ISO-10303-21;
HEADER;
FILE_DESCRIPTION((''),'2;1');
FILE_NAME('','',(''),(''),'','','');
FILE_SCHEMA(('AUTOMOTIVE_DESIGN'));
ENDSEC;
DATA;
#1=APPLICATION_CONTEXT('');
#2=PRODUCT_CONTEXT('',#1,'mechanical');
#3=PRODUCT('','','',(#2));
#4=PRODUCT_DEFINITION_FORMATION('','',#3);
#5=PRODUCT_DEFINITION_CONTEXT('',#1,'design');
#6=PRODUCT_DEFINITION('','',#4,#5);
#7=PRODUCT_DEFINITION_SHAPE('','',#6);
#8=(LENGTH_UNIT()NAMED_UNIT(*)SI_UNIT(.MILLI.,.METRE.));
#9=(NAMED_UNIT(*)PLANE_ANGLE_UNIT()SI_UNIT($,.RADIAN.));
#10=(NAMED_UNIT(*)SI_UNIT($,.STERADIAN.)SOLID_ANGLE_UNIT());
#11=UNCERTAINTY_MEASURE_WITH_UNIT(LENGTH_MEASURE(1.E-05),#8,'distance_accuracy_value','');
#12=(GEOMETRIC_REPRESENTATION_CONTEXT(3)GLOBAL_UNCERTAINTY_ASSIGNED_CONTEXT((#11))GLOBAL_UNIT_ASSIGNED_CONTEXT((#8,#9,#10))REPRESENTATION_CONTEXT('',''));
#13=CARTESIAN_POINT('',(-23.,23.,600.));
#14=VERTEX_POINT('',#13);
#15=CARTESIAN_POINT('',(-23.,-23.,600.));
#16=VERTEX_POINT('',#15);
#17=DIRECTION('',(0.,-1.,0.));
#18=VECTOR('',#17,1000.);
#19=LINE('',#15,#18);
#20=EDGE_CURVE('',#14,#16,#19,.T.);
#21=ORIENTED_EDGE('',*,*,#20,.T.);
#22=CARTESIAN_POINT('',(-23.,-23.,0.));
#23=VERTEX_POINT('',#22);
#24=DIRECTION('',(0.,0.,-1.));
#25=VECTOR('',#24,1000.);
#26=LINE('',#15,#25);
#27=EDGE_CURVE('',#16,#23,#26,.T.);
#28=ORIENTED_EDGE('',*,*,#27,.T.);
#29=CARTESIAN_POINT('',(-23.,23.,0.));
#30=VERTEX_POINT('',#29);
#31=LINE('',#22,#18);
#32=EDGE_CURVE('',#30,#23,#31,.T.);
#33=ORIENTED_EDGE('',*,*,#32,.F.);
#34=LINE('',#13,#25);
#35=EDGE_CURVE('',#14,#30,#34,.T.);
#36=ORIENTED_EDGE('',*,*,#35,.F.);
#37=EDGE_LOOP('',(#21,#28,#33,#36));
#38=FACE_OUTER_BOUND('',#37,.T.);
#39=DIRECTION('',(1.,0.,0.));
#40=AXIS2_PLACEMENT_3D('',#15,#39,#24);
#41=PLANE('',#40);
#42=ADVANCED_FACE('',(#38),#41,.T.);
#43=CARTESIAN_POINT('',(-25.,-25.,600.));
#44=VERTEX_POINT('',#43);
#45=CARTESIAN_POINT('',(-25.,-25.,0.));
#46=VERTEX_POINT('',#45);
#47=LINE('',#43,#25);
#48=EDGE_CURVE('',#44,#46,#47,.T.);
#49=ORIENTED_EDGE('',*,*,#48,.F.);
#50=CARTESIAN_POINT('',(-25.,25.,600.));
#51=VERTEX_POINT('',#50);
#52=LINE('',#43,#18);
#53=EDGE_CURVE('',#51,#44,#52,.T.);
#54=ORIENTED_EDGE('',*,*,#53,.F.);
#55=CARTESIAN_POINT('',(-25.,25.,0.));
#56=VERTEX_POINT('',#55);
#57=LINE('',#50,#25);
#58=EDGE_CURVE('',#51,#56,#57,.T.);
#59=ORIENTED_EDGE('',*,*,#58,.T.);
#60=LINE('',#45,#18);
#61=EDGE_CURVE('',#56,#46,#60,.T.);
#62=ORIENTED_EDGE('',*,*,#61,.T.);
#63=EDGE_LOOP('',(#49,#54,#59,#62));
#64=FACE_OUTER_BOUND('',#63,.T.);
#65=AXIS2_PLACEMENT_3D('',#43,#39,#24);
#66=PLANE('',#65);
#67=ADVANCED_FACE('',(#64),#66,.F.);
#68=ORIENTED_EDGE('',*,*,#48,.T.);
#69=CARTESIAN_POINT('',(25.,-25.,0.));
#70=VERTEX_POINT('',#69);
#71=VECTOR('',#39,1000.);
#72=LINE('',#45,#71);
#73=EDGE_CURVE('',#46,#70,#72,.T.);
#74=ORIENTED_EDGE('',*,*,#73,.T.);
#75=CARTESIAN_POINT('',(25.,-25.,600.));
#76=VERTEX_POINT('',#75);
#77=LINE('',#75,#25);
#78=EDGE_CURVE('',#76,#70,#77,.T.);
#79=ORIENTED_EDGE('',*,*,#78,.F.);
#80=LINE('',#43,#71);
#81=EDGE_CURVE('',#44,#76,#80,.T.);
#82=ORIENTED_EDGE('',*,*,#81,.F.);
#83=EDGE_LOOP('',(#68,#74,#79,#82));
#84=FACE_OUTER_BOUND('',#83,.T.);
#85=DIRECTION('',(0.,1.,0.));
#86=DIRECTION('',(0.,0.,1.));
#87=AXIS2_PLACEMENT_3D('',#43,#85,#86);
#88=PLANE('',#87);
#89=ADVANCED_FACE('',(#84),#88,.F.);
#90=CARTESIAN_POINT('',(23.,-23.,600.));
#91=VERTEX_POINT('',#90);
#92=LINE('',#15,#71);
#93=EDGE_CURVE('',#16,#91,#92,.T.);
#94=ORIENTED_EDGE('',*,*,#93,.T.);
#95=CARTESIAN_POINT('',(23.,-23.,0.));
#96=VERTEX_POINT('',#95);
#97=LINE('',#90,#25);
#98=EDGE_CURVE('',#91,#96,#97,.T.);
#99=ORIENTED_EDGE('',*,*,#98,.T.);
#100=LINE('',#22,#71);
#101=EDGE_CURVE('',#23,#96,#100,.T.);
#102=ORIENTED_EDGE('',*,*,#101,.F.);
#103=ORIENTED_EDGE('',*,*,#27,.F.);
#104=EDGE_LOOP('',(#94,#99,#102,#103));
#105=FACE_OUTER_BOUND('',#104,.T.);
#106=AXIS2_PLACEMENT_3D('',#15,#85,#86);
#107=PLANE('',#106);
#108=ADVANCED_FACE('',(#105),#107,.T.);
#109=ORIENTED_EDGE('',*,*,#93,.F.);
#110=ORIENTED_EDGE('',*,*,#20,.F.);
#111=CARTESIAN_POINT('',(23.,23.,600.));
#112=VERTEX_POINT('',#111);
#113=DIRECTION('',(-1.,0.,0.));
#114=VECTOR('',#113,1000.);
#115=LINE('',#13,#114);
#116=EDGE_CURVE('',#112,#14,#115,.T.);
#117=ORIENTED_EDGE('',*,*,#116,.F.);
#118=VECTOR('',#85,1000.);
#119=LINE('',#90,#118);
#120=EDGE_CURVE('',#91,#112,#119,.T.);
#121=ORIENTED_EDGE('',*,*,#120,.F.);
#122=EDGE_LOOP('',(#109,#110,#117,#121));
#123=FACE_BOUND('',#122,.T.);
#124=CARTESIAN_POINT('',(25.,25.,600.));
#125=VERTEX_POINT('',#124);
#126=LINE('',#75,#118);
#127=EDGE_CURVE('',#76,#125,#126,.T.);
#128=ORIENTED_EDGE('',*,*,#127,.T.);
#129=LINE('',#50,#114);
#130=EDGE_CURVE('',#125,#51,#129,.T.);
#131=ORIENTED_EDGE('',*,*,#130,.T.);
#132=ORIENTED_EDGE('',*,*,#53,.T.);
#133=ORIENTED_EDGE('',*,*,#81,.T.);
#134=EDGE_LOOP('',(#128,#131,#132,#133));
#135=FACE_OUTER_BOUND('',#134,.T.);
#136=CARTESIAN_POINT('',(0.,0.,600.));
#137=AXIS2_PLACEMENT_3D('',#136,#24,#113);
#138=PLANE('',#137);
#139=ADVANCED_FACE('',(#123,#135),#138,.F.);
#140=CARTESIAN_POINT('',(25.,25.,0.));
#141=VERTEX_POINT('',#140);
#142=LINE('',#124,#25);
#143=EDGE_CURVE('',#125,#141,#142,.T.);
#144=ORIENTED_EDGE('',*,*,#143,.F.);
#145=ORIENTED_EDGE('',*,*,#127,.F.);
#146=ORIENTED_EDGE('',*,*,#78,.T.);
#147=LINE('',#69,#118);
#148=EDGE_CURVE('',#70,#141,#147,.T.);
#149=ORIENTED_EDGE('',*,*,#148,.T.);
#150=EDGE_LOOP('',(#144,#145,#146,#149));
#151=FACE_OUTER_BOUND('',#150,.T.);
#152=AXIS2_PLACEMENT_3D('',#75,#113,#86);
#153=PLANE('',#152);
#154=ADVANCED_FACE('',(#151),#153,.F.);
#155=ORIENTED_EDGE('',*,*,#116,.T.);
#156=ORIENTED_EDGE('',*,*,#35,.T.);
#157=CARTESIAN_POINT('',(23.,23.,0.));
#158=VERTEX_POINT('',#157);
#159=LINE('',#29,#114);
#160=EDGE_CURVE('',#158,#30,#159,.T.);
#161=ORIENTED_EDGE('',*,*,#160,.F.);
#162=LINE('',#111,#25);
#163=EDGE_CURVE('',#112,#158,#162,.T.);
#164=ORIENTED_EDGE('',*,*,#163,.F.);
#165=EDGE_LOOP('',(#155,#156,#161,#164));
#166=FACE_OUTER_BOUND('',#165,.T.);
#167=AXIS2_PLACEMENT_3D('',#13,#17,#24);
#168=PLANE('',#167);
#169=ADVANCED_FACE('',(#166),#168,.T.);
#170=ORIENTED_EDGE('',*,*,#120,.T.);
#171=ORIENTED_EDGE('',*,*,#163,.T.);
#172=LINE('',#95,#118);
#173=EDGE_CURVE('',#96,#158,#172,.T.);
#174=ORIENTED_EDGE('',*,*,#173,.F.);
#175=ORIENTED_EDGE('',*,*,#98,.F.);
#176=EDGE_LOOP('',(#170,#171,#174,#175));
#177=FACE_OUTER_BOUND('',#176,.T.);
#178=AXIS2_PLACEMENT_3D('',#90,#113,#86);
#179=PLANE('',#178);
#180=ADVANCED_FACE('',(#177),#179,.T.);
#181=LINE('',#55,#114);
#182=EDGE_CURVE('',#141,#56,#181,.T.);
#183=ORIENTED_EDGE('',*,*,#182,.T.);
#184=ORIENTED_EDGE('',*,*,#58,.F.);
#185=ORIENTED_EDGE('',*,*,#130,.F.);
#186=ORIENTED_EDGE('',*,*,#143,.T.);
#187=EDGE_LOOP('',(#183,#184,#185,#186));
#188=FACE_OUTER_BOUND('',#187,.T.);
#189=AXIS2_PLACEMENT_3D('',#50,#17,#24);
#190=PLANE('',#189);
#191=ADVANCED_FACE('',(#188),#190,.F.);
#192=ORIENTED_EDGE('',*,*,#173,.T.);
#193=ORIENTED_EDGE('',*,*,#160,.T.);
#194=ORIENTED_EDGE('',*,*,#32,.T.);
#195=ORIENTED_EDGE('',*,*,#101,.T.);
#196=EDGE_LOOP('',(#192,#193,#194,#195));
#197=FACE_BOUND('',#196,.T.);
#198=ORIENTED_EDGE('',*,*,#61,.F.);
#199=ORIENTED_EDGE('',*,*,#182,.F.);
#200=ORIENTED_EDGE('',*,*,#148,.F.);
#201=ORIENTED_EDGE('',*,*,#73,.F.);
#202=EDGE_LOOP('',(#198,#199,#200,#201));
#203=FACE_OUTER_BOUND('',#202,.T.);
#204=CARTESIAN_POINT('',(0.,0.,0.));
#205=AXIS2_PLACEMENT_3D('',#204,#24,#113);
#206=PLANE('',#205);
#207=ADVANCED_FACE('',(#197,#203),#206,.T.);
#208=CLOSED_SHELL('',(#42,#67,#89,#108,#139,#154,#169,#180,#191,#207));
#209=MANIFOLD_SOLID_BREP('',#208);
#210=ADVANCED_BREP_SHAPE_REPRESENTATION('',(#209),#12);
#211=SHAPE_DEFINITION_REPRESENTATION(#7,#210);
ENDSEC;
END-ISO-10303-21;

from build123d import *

# Parameters (mm, degrees)
SKETCH1_W           = 50
SKETCH1_H           = 50
SKETCH1_W_2         = 46
SKETCH1_H_2         = 46
BOSS_EXTRUDE1_DEPTH = 600


with BuildPart() as part:
    # Sketch1 → Boss-Extrude1 (new body)
    with BuildSketch(Plane.XY):
        Rectangle(SKETCH1_W, SKETCH1_H)
        Rectangle(SKETCH1_W_2, SKETCH1_H_2, mode=Mode.SUBTRACT)
    extrude(amount=BOSS_EXTRUDE1_DEPTH)


solid = part.part
